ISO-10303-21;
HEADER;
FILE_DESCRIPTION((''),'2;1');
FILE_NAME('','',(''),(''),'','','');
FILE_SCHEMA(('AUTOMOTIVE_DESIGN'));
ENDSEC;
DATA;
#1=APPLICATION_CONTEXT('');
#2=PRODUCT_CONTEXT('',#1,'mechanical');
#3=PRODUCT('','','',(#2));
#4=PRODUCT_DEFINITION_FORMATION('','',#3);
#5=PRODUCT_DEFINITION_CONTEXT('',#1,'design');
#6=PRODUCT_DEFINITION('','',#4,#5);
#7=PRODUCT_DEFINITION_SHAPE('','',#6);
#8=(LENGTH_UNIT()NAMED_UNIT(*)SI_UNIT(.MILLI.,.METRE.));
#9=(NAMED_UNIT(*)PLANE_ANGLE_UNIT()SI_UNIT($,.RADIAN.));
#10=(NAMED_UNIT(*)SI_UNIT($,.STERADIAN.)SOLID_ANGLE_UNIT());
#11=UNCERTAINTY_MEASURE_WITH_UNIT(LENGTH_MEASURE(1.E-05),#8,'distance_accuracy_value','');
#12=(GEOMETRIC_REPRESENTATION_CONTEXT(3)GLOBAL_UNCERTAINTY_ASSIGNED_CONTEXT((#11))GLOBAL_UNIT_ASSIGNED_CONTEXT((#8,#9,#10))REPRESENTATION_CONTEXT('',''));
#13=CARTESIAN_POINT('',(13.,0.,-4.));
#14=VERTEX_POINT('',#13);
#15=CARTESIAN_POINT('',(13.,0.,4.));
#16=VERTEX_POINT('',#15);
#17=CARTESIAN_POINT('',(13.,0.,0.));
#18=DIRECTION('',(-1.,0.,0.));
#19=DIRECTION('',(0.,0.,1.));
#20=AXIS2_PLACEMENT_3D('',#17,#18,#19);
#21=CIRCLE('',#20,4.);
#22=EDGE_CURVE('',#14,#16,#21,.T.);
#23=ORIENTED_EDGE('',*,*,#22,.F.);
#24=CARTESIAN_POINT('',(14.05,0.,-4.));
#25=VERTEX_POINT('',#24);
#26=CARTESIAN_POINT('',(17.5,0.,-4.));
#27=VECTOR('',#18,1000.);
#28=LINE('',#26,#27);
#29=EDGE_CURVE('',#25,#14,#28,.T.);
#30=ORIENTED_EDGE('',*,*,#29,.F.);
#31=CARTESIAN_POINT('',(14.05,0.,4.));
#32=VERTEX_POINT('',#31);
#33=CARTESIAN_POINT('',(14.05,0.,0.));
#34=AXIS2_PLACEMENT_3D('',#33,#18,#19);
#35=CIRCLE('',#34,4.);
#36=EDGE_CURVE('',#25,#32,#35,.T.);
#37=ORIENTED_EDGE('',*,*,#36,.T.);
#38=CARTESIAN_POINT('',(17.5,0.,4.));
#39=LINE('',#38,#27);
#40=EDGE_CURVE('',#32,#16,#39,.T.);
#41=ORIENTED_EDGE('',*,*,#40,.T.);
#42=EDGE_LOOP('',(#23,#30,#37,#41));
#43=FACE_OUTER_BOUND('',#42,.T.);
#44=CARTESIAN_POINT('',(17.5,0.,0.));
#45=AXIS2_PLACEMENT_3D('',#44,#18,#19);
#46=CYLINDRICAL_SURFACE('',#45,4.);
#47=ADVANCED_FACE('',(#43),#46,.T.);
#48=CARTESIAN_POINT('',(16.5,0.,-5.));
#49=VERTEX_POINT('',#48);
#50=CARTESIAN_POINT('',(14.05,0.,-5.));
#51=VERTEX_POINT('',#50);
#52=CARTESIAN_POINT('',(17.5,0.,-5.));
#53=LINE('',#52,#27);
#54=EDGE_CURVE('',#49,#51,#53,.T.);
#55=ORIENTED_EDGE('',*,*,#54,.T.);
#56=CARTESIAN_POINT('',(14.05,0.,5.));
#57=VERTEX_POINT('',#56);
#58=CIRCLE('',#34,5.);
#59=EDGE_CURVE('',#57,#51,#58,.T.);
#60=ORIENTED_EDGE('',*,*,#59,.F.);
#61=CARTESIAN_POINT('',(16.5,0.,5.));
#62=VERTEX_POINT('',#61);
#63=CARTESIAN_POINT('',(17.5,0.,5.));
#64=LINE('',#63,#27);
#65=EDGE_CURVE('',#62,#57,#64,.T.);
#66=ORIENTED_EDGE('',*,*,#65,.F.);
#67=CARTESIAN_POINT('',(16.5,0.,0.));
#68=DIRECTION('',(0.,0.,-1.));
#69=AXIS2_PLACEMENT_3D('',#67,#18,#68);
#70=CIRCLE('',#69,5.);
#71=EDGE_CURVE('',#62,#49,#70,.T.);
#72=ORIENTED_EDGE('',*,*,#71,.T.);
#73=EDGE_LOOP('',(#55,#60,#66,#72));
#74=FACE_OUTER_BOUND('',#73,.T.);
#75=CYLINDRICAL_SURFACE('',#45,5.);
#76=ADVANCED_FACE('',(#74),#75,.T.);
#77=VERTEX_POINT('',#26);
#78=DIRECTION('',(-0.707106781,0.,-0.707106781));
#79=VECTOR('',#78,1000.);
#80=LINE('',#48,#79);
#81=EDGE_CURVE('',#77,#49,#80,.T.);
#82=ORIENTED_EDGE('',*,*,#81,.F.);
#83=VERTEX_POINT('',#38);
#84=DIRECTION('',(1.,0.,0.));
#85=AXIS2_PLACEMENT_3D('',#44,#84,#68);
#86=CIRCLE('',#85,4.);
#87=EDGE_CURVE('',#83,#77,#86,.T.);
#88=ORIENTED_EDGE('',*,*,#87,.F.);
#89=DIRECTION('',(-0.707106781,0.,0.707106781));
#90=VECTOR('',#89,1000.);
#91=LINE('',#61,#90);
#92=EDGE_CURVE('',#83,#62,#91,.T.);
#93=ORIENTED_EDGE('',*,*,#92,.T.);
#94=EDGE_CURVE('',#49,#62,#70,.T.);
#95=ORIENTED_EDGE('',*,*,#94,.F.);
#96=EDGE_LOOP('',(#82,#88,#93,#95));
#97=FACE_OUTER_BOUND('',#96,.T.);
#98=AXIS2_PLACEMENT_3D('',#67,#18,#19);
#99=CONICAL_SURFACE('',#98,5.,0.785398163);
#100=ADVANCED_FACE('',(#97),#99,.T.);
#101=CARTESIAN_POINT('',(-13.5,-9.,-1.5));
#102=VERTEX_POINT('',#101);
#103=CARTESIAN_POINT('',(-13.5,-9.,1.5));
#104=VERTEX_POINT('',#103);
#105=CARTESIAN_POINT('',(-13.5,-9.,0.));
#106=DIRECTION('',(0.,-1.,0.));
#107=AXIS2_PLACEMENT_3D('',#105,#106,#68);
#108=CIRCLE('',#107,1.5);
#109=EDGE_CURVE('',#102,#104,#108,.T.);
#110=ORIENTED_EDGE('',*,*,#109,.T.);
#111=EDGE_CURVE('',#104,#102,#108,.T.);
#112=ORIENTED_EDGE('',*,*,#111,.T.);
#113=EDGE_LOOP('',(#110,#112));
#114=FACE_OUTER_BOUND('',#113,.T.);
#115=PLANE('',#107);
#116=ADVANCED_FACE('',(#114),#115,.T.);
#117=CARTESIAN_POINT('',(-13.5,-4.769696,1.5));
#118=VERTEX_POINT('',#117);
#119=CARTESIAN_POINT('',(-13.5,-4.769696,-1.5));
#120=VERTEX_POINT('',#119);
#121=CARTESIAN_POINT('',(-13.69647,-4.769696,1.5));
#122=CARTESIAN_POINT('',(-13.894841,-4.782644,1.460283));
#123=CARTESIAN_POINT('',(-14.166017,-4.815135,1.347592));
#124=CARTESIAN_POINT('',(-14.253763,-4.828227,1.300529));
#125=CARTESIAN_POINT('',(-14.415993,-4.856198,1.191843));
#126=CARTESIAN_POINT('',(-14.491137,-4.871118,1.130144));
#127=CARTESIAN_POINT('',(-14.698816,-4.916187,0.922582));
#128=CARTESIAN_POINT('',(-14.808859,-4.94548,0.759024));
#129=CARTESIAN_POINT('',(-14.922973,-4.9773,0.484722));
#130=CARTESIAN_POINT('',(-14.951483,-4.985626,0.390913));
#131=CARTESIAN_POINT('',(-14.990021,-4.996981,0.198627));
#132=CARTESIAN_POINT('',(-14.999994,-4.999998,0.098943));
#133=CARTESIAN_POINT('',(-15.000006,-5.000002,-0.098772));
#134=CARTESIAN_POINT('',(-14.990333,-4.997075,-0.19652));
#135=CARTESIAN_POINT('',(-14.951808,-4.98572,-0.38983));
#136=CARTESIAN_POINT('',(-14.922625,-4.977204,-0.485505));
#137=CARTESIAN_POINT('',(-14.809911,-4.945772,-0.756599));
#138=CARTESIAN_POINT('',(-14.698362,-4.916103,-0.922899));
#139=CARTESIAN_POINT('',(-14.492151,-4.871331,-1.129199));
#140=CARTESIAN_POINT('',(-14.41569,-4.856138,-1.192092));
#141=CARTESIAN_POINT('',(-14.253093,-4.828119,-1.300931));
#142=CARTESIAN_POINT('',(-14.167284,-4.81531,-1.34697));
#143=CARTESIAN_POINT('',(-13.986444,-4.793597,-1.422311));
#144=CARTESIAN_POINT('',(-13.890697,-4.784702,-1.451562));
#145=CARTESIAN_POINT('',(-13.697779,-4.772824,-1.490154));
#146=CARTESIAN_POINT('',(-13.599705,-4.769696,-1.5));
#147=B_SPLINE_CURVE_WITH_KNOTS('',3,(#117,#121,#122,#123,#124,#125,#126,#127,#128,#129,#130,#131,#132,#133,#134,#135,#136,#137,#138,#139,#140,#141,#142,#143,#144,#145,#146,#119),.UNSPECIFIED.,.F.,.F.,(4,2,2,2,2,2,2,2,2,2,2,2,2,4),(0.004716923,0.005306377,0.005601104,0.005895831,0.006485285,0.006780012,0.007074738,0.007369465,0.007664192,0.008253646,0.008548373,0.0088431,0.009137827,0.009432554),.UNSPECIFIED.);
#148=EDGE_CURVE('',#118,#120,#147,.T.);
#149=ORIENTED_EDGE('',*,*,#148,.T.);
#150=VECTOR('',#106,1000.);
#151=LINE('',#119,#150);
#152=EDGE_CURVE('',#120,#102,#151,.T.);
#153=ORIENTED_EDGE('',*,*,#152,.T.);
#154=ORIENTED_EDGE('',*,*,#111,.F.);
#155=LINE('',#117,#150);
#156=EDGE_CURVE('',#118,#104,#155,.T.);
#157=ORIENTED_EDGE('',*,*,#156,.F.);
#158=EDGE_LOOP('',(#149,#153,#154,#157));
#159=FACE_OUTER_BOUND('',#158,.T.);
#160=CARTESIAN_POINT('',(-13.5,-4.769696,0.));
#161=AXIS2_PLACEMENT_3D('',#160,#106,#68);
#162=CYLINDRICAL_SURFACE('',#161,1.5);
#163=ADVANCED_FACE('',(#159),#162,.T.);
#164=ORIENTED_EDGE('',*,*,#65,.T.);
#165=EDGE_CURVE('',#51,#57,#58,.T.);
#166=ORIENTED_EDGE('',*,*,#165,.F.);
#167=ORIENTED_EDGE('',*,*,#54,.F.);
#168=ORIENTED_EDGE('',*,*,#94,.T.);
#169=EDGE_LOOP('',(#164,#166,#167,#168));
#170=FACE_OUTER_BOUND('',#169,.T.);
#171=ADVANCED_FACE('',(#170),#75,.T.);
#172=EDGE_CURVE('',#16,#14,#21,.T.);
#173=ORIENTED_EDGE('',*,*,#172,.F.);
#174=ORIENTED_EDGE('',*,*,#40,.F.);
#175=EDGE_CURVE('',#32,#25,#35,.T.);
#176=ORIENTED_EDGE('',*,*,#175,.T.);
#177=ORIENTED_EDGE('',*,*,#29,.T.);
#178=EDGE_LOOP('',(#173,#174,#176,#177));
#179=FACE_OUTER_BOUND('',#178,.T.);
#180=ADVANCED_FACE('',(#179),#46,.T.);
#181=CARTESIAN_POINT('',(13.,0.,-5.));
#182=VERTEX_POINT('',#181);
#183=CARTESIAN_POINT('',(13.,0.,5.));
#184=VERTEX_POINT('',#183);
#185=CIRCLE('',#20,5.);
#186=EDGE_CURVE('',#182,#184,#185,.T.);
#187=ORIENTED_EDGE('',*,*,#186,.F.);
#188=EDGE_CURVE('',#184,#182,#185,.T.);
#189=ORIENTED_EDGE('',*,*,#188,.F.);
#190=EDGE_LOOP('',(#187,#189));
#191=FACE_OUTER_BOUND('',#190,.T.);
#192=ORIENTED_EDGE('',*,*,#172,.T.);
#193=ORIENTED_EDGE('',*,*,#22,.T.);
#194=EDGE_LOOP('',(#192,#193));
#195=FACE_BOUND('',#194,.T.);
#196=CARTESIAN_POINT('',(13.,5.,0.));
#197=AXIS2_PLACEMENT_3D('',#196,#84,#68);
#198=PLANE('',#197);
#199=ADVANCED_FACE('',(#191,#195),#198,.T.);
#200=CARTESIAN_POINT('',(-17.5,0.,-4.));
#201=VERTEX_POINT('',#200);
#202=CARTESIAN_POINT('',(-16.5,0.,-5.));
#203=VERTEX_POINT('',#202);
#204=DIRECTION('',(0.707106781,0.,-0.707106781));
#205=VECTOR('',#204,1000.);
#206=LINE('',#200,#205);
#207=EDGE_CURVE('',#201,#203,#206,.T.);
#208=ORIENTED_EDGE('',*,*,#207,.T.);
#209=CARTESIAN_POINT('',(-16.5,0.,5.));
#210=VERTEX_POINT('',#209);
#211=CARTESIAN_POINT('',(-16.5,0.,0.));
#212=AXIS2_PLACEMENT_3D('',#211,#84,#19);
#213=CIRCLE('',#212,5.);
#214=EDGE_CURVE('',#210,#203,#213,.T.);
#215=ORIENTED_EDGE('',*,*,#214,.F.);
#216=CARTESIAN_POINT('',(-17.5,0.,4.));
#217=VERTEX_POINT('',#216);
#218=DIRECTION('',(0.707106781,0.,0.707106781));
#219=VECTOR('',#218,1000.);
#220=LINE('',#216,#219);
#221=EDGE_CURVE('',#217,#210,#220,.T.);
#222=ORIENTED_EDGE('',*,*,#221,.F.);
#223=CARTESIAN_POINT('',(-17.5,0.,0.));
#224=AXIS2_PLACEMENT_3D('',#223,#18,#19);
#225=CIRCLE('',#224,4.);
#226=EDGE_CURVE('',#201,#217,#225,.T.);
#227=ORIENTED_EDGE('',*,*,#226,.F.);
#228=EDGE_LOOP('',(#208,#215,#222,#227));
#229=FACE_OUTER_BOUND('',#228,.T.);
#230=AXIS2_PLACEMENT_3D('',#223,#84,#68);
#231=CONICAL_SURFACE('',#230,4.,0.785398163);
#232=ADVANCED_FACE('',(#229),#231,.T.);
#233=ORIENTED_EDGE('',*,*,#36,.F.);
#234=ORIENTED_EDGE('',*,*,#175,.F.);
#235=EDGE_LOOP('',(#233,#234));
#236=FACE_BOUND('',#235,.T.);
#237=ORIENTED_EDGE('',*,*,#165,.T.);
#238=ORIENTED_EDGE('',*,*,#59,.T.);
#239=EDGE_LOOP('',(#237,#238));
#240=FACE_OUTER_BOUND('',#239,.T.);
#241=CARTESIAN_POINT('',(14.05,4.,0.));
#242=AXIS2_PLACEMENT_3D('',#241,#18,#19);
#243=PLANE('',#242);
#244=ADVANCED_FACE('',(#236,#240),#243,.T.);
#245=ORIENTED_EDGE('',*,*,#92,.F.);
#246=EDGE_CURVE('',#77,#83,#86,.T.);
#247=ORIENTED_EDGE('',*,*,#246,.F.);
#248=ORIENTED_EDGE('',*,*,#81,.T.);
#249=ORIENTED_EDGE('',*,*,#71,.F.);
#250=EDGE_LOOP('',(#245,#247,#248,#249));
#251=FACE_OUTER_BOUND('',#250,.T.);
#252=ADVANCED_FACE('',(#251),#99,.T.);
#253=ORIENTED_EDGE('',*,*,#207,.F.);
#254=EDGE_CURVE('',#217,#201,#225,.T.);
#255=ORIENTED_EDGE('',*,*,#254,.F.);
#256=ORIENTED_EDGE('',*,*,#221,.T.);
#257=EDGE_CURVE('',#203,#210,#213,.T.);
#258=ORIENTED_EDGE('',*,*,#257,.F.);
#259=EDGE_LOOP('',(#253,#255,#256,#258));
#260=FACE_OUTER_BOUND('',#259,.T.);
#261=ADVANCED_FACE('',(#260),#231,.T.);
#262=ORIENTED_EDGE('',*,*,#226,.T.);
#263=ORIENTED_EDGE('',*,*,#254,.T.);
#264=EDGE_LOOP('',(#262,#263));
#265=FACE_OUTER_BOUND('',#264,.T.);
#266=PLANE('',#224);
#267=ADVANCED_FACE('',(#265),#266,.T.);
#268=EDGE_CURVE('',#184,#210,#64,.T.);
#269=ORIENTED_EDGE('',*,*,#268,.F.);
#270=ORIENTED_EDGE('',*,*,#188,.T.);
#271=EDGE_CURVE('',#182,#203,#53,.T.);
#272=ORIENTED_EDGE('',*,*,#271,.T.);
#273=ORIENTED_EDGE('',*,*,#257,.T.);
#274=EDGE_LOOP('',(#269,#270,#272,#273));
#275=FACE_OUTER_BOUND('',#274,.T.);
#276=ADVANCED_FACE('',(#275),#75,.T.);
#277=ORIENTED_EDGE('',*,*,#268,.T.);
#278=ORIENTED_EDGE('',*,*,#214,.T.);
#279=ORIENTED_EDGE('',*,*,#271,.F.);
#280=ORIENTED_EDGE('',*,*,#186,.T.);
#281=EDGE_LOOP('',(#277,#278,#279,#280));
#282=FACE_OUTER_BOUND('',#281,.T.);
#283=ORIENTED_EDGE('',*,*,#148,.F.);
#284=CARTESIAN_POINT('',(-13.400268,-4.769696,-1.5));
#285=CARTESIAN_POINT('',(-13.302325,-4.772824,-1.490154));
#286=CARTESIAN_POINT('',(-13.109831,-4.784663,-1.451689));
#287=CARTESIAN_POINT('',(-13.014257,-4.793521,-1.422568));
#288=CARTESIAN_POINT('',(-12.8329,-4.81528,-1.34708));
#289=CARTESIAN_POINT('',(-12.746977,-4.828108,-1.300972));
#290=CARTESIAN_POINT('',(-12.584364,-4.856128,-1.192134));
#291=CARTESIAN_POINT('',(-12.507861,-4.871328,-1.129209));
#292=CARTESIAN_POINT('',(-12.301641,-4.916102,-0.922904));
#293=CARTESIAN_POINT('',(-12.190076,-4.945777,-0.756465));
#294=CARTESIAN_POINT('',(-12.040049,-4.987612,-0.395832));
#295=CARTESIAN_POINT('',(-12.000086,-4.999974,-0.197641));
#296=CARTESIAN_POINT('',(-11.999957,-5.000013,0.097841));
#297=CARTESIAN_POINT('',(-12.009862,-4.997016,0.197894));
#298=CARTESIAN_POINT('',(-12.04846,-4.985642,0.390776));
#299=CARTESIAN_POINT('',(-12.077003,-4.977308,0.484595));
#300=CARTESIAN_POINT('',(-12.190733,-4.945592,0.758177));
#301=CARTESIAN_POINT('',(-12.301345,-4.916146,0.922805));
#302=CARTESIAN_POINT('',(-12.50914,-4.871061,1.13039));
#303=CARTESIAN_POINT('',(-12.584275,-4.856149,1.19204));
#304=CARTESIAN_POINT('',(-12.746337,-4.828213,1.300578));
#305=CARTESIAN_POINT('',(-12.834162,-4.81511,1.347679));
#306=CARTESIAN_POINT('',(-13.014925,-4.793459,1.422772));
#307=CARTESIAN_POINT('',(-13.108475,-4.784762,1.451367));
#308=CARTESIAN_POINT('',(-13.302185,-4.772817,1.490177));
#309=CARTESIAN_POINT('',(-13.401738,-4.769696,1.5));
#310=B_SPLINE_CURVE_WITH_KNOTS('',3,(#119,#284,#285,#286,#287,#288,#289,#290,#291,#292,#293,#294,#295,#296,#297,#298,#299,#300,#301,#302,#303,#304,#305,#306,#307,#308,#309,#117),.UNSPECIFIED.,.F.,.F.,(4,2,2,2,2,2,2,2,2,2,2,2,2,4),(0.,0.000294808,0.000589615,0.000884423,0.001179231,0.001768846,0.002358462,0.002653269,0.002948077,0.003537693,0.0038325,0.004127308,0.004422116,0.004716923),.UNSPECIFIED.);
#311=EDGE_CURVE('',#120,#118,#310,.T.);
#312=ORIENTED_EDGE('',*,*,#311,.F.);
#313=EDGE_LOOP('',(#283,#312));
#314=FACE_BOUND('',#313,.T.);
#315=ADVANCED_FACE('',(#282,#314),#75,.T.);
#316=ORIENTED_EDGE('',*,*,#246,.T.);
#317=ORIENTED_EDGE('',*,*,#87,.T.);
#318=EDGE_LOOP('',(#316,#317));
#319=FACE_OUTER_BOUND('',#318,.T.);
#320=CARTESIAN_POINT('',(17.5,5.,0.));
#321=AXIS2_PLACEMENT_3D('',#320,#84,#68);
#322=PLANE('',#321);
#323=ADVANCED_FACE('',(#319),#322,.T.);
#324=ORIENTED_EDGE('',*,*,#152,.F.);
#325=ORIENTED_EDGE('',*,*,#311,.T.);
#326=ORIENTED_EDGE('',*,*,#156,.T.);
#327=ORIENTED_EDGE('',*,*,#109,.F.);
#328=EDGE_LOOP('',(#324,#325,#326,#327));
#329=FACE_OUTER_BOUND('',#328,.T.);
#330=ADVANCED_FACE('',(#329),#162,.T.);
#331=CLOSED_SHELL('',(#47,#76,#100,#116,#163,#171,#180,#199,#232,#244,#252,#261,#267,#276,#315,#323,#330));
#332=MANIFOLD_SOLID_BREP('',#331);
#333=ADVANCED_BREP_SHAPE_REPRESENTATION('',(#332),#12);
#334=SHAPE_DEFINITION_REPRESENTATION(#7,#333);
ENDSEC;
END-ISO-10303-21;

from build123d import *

# Parameters (mm, degrees)
SKETCH_2_W     = 1.5
SKETCH_2_H     = 4.230303993
CHAMFER_1_SIZE = 1


with BuildPart() as part:
    # 草图1 → 旋转1 (revolve)
    with BuildSketch(Plane(origin=(0, 0, 0), x_dir=(-1, 0, 0), z_dir=(0, 0, -1)), mode=Mode.PRIVATE) as revolve_1_sk:
        Polygon((-17.5, 5), (-17.5, 0), (17.5, 0), (17.5, 5), (-13, 5), (-13, 4), (-14.05, 4), (-14.05, 5), align=None)
    revolve(revolve_1_sk.sketch.rotate(Axis((17.5, 0, 0), (-1, 0, 0)), 270), axis=Axis((17.5, 0, 0), (-1, 0, 0)))

    # 草图2 → 旋转2 (revolve)
    with BuildSketch(Plane(origin=(-13.5, 0, 0), x_dir=(0, 0, -1), z_dir=(1, 0, 0))):
        with Locations((0.75, -6.884848004)):
            Rectangle(SKETCH_2_W, SKETCH_2_H)
    revolve(axis=Axis((-13.5, -4.769696007, 0), (0, -1, 0)))

    # 倒角1
    chamfer_1_edges = [part.edges().sort_by_distance(p)[0] for p in [
        (17.5, 0, -5),
        (-17.5, 0, -5),
    ]]
    chamfer(chamfer_1_edges, length=CHAMFER_1_SIZE)


solid = part.part
